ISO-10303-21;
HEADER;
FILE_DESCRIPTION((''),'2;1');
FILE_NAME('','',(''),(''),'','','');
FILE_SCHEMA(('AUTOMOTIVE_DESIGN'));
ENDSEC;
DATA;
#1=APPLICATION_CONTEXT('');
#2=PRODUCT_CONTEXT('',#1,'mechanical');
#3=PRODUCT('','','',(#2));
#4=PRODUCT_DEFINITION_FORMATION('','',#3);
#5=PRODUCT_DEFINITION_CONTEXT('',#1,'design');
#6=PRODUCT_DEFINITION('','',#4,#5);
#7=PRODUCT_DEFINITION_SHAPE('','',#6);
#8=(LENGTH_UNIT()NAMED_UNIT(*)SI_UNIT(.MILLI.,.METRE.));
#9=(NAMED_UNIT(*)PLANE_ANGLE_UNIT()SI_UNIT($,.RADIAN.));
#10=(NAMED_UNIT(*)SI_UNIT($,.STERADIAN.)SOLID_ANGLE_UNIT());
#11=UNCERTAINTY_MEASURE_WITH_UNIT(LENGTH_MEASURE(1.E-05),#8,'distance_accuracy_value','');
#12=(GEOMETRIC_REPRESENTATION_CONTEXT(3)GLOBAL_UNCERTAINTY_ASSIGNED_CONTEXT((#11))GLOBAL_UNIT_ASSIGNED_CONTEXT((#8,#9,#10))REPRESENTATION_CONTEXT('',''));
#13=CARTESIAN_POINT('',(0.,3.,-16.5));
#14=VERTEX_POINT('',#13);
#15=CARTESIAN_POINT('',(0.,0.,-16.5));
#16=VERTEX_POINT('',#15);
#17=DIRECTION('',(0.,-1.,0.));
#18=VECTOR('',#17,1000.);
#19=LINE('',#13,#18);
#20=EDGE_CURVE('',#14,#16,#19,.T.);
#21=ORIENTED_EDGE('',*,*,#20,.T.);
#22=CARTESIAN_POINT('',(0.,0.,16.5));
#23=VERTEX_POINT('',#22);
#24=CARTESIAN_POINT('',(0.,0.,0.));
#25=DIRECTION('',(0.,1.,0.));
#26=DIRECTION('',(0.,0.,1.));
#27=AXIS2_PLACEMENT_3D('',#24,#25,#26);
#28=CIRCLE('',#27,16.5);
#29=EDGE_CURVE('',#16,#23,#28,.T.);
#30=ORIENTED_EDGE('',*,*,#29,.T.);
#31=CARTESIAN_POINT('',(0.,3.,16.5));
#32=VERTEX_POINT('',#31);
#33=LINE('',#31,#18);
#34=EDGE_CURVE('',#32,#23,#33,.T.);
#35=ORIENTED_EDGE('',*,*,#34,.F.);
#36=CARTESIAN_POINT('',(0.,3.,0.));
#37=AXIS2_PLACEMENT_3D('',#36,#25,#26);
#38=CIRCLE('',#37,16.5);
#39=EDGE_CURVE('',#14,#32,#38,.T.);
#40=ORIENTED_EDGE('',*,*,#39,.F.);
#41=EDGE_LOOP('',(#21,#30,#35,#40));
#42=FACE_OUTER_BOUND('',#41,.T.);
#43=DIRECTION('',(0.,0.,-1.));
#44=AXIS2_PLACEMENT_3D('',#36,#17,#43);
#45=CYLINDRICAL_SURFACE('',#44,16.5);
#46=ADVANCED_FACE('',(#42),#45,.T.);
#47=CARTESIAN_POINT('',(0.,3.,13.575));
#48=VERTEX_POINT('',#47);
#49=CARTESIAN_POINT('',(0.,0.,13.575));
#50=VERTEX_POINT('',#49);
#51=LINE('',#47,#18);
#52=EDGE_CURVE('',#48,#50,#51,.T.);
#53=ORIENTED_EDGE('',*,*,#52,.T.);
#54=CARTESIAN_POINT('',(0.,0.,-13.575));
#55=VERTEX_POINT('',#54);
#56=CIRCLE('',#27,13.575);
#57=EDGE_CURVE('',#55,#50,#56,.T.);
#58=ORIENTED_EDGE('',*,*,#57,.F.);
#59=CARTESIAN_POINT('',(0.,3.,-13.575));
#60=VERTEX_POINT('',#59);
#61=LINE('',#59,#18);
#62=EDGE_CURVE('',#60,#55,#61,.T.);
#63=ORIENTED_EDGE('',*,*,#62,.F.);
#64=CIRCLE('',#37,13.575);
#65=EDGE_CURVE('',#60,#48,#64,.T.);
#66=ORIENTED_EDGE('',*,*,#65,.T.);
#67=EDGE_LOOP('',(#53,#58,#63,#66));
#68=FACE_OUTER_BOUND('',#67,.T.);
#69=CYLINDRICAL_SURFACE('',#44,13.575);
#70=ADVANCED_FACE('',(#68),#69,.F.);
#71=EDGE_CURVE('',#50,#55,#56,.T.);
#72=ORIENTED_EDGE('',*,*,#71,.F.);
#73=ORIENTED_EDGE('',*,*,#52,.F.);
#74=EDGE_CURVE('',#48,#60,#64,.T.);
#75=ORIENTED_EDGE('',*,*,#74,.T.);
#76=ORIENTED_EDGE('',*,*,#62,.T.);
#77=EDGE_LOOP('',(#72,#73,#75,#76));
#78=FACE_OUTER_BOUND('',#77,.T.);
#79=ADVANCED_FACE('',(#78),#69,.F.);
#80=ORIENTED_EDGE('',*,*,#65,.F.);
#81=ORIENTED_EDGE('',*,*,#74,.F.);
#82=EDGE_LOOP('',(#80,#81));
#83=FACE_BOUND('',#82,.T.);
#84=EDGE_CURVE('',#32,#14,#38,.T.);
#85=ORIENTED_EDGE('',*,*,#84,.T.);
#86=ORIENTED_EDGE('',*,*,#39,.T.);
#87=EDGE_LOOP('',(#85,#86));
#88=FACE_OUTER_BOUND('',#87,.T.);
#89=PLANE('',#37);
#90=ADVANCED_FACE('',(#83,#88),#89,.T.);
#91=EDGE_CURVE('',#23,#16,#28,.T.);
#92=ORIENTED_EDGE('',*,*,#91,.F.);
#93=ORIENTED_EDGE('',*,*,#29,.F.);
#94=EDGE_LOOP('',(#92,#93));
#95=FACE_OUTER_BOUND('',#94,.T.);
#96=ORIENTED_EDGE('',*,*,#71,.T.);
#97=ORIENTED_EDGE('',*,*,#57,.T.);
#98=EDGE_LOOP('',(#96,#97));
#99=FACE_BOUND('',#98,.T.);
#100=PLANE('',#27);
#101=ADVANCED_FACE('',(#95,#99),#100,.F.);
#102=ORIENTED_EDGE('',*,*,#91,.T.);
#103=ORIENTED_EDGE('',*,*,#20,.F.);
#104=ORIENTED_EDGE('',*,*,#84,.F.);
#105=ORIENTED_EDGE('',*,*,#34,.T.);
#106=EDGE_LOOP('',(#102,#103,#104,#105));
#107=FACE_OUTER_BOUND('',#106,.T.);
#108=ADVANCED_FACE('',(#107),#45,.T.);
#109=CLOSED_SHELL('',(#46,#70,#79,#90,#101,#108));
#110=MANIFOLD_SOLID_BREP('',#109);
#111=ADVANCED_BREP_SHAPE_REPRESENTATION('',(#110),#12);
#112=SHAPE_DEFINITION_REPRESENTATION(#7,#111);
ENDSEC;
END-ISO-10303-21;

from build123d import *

# Parameters (mm, degrees)
SKETCH_1_R      = 16.5
SKETCH_1_R_2    = 13.575
EXTRUDE_1_DEPTH = 3


with BuildPart() as part:
    # 草图1 → 凸台-拉伸1 (new body)
    with BuildSketch(Plane(origin=(0, 0, 0), x_dir=(1, 0, 0), z_dir=(0, 1, 0))):
        with Locations(Location((0, 0, 0), (0, 0, 270))):
            Circle(SKETCH_1_R)
        with Locations(Location((0, 0, 0), (0, 0, 270))):
            Circle(SKETCH_1_R_2, mode=Mode.SUBTRACT)
    extrude(amount=EXTRUDE_1_DEPTH)


solid = part.part
